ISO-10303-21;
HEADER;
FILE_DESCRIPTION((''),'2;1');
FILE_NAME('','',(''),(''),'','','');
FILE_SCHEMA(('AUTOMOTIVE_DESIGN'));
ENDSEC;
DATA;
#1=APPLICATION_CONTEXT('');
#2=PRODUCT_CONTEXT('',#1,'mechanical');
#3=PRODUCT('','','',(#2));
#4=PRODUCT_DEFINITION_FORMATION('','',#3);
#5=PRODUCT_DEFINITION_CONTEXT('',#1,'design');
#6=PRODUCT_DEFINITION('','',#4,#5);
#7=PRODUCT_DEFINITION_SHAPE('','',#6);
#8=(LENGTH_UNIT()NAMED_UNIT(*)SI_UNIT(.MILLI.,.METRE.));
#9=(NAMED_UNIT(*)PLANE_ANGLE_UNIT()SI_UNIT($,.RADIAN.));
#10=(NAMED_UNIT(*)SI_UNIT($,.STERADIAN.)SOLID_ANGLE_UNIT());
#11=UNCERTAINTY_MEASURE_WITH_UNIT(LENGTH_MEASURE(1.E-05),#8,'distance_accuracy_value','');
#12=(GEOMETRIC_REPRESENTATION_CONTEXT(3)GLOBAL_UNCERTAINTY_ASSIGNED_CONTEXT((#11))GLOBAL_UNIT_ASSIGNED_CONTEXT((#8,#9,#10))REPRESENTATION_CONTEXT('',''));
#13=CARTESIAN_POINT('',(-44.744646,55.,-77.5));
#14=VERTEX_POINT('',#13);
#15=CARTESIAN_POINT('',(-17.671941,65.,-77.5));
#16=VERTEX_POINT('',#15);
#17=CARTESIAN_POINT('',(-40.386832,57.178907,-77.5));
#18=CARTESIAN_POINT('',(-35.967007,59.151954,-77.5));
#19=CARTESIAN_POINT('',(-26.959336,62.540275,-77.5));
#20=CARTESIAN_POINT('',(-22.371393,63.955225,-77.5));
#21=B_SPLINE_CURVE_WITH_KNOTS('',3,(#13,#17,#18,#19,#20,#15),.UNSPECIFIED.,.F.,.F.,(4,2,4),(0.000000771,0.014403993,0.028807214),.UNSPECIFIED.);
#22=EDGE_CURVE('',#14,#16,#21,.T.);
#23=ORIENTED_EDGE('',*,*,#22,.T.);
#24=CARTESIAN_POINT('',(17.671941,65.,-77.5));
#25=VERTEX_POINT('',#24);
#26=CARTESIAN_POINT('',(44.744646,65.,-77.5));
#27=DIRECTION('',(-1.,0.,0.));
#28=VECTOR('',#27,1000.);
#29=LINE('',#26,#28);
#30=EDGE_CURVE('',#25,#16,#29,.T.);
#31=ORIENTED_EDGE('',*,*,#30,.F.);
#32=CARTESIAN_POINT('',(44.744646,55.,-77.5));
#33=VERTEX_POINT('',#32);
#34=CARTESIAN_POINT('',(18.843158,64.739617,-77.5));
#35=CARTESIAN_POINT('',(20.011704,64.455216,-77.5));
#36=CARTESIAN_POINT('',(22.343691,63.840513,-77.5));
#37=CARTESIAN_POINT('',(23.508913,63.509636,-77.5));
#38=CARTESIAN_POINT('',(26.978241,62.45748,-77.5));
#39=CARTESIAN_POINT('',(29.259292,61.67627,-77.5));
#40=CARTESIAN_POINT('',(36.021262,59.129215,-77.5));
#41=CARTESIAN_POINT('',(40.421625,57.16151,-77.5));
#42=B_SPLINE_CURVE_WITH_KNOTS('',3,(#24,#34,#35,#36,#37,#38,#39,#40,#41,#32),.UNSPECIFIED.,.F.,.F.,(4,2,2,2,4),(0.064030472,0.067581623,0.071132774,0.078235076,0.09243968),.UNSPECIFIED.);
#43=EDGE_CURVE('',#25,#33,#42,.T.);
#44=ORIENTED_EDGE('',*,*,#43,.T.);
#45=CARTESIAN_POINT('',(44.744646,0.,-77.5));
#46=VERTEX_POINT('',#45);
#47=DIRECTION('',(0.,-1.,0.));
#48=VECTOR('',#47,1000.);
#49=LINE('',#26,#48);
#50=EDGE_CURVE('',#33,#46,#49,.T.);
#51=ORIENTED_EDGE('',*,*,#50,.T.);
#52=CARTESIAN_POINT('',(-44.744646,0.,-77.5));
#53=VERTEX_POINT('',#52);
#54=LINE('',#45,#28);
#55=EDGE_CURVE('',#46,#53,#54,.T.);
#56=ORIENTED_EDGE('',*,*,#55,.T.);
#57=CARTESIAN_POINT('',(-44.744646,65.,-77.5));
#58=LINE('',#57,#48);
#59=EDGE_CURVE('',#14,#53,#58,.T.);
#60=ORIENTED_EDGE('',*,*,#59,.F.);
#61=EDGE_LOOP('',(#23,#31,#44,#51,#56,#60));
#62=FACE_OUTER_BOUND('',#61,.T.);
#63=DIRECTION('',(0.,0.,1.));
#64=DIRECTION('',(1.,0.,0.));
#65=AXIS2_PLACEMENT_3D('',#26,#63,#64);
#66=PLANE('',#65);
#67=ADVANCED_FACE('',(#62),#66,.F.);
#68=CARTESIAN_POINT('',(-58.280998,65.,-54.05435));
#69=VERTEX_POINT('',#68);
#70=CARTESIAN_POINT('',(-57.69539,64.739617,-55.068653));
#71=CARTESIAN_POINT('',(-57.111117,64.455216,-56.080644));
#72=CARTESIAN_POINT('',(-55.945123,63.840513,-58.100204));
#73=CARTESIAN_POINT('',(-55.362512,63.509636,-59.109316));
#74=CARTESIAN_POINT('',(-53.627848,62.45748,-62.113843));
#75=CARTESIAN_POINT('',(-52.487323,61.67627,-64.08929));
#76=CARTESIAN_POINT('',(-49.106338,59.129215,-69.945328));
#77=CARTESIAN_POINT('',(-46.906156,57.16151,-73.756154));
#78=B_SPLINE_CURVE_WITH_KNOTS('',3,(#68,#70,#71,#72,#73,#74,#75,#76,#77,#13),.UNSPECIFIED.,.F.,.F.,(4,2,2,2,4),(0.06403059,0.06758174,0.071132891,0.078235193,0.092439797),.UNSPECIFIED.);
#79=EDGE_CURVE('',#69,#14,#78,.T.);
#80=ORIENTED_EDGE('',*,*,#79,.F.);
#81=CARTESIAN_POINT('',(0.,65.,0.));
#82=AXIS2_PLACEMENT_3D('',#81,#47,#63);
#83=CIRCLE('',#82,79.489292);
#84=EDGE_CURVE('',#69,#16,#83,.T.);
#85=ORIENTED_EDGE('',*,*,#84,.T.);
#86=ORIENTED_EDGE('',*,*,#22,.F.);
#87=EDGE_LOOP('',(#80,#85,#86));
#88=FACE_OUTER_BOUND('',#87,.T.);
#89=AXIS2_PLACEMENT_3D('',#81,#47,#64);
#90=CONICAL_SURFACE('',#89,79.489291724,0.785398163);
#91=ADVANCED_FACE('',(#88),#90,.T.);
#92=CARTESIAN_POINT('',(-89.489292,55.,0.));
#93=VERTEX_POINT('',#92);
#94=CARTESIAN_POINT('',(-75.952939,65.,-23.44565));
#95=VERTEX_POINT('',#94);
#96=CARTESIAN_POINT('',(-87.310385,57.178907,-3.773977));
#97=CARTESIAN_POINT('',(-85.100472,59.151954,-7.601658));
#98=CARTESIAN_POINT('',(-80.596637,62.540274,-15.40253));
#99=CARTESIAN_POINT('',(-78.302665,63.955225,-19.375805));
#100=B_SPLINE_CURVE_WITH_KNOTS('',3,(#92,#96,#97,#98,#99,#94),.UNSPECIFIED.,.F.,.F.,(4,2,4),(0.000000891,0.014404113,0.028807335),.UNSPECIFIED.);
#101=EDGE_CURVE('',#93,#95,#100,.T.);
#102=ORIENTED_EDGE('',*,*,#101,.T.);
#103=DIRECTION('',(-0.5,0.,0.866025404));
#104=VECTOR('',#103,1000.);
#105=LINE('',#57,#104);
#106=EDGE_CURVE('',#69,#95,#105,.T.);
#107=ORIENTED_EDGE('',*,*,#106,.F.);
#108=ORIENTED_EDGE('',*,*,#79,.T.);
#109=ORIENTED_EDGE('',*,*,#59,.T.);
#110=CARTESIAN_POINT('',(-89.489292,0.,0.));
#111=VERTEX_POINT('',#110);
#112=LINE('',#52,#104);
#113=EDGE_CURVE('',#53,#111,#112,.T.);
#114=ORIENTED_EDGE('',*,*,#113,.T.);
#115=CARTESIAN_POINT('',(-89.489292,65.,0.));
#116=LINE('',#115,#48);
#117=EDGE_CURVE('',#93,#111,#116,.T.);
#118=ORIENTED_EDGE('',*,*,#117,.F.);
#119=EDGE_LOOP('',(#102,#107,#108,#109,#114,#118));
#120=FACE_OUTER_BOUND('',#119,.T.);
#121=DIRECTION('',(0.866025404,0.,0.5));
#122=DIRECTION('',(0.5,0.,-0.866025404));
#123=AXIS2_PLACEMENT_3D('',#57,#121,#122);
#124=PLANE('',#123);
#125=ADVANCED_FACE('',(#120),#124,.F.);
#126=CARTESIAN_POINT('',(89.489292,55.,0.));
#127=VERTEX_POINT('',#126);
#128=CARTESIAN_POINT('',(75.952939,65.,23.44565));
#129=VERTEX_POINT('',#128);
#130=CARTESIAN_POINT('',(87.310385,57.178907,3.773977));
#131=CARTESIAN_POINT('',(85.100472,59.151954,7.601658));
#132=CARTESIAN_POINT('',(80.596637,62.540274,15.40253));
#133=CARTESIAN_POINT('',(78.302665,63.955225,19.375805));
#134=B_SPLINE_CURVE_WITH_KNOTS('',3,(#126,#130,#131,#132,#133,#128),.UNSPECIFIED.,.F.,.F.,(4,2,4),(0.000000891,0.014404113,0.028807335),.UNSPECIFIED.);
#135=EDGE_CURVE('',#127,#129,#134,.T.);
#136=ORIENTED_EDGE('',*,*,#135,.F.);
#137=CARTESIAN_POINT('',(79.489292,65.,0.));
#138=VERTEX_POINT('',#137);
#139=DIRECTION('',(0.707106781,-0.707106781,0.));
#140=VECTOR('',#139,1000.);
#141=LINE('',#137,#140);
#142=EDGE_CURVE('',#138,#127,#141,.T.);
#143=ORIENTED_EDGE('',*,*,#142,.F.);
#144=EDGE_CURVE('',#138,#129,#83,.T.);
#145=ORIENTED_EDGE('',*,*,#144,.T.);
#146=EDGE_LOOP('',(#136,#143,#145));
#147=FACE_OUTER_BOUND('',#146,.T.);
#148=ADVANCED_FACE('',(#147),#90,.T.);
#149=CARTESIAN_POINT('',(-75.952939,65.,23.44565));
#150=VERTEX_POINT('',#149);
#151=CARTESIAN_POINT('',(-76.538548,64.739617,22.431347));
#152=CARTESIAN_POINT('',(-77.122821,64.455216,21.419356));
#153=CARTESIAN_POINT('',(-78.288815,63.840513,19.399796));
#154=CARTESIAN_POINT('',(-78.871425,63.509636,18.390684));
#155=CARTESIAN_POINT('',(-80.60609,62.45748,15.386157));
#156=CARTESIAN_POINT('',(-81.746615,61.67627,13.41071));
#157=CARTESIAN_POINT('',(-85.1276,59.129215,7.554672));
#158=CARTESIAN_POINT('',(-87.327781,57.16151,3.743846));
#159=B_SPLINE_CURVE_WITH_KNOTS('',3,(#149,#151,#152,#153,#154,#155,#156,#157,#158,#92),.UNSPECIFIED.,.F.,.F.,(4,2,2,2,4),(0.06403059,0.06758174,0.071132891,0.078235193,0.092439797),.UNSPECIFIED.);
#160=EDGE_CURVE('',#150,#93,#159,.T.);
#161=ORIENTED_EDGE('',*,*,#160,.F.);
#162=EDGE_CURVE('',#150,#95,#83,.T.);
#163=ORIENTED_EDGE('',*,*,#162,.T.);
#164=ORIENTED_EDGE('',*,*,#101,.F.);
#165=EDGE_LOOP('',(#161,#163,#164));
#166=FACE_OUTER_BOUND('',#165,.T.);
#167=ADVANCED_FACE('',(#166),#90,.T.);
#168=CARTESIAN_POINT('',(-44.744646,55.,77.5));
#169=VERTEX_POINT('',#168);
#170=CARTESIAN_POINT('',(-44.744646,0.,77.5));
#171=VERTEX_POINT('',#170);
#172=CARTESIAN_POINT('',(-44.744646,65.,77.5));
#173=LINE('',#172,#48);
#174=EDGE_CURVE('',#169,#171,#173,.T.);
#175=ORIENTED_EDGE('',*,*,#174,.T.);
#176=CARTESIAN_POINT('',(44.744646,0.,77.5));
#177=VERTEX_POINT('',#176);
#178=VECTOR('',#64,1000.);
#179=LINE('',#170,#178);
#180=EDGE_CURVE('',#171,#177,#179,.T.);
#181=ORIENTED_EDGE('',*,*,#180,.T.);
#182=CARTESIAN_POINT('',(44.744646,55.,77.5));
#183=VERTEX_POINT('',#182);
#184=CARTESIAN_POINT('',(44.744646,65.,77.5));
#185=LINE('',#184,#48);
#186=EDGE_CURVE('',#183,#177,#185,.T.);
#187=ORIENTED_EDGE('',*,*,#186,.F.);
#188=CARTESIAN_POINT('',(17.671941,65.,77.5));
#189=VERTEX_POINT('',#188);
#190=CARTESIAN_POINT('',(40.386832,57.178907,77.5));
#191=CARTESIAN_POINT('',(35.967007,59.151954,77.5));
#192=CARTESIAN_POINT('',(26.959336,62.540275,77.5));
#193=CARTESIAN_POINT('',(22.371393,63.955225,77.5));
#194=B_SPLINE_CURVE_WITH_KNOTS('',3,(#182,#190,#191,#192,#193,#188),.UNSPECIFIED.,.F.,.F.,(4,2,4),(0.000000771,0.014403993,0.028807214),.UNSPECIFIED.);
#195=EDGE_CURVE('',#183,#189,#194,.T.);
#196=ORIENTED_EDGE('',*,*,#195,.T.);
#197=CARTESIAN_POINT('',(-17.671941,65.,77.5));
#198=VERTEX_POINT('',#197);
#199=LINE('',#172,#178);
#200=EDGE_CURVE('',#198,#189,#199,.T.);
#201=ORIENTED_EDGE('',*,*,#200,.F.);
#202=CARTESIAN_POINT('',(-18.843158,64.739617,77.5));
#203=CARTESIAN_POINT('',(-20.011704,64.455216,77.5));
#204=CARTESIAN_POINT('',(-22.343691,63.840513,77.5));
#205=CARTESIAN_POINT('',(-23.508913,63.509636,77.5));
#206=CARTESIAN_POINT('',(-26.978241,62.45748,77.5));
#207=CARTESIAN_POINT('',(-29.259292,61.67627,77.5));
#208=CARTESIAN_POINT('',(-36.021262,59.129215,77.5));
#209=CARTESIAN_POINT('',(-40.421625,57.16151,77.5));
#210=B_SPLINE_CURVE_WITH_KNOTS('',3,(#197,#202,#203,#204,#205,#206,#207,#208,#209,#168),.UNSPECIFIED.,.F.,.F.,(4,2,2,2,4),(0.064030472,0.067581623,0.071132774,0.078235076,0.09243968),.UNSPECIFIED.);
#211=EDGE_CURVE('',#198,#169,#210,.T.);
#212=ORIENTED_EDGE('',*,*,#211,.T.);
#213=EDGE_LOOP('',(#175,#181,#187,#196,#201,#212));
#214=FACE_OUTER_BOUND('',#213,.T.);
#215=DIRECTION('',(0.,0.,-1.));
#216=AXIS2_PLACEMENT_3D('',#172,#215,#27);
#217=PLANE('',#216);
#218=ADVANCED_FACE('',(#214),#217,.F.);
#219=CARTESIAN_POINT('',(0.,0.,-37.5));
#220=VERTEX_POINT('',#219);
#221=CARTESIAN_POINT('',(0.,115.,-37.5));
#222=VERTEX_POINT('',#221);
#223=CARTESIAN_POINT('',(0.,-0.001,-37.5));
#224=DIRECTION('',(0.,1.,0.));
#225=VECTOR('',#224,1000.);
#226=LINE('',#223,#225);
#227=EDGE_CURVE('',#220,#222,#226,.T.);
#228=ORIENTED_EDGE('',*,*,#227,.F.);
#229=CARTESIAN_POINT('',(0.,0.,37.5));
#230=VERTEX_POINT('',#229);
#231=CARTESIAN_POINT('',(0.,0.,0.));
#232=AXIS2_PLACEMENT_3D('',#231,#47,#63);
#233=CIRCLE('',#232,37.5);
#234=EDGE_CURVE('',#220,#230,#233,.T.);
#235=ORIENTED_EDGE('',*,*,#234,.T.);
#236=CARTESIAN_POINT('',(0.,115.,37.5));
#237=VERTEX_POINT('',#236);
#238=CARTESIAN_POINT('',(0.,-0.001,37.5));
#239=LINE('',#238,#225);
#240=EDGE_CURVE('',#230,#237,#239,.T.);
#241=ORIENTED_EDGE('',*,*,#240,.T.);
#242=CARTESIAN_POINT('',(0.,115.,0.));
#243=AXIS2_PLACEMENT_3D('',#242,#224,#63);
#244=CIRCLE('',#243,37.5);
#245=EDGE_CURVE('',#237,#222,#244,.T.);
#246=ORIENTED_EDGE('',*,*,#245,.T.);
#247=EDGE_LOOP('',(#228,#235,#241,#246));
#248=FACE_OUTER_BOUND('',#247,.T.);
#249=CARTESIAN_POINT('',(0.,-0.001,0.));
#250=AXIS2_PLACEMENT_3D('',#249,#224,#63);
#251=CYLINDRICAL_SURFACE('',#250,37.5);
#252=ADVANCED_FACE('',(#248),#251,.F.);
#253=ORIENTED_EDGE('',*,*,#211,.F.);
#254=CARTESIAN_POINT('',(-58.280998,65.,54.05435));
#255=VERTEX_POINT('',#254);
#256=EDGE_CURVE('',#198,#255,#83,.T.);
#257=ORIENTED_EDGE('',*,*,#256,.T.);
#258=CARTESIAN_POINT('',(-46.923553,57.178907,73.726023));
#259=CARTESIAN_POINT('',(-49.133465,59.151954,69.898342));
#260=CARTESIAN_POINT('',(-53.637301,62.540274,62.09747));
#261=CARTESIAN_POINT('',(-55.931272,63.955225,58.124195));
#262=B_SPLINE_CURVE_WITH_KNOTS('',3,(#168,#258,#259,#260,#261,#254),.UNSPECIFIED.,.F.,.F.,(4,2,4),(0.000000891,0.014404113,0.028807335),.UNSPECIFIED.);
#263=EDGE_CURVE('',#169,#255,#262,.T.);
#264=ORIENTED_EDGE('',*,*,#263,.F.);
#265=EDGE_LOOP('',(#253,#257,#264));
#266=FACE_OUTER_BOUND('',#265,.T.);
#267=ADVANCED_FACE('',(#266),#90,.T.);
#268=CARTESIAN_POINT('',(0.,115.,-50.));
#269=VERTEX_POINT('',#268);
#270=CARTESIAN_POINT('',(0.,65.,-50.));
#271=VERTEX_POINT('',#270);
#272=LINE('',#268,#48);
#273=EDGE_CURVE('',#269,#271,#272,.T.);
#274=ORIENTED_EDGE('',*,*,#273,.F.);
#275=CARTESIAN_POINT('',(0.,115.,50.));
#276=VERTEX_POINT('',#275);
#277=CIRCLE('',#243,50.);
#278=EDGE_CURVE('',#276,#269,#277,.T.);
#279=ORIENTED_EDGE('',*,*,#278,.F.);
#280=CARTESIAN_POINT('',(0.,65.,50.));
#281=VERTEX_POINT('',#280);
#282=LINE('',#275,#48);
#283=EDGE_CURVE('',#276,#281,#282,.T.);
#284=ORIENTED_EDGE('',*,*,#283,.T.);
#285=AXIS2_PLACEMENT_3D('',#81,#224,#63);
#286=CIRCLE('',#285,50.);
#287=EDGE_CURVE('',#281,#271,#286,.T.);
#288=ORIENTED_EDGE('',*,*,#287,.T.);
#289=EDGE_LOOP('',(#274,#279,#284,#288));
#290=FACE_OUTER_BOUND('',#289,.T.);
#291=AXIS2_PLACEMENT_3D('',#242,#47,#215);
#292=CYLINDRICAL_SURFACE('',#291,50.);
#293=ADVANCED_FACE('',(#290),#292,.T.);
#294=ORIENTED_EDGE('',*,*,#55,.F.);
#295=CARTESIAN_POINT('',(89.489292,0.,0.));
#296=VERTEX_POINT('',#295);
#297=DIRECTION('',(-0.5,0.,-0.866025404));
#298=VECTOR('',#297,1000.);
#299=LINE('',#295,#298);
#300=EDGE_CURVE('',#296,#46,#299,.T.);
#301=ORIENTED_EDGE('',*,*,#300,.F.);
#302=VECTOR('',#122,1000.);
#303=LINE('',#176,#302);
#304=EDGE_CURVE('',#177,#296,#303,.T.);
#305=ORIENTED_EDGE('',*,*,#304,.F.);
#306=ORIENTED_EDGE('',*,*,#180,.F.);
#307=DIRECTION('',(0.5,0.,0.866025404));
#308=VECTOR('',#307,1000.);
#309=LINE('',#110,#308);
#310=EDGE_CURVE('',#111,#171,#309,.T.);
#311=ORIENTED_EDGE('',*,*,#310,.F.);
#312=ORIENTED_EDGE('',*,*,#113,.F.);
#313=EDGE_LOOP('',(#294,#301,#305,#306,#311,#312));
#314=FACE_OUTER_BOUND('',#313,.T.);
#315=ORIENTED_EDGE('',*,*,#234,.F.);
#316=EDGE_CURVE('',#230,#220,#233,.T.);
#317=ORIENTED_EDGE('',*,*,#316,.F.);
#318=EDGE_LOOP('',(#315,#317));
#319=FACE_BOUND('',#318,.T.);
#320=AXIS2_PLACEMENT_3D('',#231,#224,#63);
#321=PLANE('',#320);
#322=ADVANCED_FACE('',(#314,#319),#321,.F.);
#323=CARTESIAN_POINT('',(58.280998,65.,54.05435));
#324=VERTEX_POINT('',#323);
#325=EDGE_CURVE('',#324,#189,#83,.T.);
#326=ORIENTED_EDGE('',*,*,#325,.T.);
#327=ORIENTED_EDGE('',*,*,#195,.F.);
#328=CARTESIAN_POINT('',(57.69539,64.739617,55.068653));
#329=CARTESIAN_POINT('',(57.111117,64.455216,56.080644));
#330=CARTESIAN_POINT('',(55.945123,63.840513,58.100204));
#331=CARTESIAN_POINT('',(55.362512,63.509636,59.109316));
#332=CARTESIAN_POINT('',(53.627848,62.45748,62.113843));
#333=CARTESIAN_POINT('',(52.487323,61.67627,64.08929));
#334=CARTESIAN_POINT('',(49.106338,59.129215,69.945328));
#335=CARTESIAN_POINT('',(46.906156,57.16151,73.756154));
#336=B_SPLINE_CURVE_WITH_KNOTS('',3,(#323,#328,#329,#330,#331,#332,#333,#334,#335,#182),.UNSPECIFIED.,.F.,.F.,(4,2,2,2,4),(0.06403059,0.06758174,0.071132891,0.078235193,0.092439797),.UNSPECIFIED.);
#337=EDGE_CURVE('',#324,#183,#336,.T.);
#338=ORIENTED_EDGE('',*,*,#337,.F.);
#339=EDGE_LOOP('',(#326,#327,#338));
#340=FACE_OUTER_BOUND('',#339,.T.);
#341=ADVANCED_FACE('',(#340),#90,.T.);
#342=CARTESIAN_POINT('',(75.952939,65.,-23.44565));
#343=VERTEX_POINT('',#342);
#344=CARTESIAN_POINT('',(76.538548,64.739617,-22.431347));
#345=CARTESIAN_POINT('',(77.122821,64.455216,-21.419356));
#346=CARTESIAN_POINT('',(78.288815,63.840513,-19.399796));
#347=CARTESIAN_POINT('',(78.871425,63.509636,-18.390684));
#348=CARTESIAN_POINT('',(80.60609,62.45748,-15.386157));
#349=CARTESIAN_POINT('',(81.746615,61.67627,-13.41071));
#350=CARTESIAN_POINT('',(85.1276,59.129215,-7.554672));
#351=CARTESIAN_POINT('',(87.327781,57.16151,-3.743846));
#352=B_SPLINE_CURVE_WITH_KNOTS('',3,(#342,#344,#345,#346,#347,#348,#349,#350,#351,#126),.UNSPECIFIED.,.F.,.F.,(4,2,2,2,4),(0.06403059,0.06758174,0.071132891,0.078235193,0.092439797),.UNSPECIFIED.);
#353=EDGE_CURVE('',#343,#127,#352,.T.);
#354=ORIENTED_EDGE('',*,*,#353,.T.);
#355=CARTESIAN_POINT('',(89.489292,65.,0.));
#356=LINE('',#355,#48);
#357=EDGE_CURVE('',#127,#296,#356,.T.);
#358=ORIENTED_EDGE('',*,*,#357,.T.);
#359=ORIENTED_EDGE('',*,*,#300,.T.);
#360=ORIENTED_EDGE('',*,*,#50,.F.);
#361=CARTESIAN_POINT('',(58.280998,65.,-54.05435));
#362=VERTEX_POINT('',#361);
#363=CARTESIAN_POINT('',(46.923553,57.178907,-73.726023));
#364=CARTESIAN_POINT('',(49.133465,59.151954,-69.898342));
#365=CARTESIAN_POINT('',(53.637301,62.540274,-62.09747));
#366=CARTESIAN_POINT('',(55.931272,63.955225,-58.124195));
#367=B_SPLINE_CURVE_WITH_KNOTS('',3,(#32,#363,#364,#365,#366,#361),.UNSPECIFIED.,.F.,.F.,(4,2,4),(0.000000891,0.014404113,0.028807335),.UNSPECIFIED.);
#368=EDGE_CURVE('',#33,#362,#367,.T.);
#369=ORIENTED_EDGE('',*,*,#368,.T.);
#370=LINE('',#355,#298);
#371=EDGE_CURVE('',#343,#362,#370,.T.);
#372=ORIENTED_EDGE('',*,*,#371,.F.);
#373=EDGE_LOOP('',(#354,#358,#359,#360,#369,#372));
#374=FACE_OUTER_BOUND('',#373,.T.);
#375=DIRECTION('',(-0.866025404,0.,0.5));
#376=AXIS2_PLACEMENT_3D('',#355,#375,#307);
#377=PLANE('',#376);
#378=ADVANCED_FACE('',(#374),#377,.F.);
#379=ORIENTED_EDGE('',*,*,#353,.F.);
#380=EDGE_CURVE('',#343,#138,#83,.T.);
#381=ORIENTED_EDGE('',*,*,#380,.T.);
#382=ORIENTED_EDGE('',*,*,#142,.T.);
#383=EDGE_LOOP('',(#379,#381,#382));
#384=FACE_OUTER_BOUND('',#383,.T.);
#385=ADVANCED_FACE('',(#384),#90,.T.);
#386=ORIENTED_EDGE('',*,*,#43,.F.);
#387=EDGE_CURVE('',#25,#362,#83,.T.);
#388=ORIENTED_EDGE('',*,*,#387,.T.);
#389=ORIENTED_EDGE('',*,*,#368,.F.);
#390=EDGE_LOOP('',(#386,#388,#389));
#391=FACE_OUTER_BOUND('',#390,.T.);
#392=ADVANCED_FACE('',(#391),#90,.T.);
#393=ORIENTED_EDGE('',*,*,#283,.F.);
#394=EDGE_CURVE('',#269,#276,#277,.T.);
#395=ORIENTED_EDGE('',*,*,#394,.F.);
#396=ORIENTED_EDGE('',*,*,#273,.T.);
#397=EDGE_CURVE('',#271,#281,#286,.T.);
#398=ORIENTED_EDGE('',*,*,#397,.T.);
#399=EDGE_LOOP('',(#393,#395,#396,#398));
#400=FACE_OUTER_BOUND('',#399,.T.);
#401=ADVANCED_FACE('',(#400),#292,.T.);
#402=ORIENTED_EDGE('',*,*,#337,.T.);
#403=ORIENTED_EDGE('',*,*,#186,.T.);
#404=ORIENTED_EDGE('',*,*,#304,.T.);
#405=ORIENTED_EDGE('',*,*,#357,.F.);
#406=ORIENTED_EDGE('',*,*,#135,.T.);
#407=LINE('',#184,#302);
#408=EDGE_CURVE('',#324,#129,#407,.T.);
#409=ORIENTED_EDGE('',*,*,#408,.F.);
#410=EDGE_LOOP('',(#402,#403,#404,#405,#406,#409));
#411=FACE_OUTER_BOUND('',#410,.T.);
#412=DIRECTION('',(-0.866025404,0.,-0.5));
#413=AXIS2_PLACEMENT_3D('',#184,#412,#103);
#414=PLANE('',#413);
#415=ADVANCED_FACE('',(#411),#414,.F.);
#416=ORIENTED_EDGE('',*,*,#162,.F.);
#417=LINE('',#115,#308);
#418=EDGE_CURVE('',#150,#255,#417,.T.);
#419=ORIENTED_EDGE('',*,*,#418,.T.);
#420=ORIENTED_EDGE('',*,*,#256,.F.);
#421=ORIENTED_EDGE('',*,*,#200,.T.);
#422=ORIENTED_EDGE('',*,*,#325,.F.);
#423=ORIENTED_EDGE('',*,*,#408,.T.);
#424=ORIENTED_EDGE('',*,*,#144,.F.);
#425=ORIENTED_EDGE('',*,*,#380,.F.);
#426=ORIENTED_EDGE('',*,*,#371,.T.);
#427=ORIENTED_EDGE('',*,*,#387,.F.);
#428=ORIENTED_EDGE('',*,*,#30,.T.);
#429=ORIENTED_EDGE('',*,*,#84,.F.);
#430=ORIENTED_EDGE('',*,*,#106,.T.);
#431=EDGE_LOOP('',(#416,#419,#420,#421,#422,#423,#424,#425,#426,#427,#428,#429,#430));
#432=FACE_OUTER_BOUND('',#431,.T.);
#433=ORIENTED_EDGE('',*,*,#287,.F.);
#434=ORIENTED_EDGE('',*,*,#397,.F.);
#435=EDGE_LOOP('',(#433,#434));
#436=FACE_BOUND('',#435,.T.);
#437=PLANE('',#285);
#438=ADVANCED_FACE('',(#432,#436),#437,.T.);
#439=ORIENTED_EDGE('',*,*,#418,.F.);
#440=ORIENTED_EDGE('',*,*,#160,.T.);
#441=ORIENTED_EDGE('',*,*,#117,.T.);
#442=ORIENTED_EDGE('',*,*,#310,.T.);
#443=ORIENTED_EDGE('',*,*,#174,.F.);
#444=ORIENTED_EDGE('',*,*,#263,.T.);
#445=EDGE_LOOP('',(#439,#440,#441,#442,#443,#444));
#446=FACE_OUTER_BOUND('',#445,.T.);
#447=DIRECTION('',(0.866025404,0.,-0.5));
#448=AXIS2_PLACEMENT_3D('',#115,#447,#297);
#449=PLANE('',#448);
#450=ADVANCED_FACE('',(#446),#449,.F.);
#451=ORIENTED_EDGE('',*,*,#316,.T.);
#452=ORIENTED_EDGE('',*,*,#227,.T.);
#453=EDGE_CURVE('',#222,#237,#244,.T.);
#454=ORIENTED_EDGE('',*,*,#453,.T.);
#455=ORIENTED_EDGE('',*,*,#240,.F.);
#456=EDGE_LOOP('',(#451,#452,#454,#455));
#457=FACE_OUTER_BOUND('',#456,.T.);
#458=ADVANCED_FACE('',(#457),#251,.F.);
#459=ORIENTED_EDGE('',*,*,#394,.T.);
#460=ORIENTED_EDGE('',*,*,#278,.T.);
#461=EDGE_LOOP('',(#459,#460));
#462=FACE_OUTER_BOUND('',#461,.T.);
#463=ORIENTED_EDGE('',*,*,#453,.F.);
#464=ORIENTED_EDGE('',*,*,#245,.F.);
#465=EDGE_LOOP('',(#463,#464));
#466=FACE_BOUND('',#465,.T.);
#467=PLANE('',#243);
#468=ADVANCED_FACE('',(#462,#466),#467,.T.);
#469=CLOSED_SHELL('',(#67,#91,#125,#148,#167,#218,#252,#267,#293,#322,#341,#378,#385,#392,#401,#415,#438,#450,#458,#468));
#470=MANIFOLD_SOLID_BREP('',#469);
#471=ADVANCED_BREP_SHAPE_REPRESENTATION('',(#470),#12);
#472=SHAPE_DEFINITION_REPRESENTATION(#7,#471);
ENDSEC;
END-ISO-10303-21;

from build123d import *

# Parameters (mm, degrees)
HEX_BODY_155AF_X65_DEPTH = 65
COLLAR_PROFILE_100_R     = 50
COLLAR_100_X50_DEPTH     = 50
THROUGH_BORE_75_REACH    = 167.044
BORE_PROFILE_75_R        = 37.5


with BuildPart() as part:
    # Hex Profile 155AF → Hex Body 155AF x65 (new body)
    with BuildSketch(Plane(origin=(0, 0, 0), x_dir=(1, 0, 0), z_dir=(0, 1, 0))):
        Polygon((89.489291724, 0), (44.744645862, 77.5), (-44.744645862, 77.5), (-89.489291724, 0), (-44.744645862, -77.5), (44.744645862, -77.5), align=None)
    extrude(amount=HEX_BODY_155AF_X65_DEPTH)

    # Hex Chamfer Profile 10x10 → Hex Corner Chamfer 10x10 (revolve, cut)
    with BuildSketch(Plane.XY):
        Polygon((79.489291724, 65), (89.489291724, 65), (89.489291724, 55), align=None)
    revolve(axis=Axis((0, 0, 0), (0, 1, 0)), mode=Mode.SUBTRACT)

    # Collar Profile Ø100 → Collar Ø100 x50 (add)
    with BuildSketch(Plane(origin=(0, 65, 0), x_dir=(1, 0, 0), z_dir=(0, 1, 0))):
        with Locations(Location((0, 0, 0), (0, 0, 270))):
            Circle(COLLAR_PROFILE_100_R)
    extrude(amount=COLLAR_100_X50_DEPTH)

    # Bore Profile Ø75 → Through Bore Ø75 (cut, up to next)
    with BuildSketch(Plane(origin=(0, 115, 0), x_dir=(1, 0, 0), z_dir=(0, 1, 0)), mode=Mode.PRIVATE) as through_bore_75_sk1:
        with Locations(Location((0, 0, 0), (0, 0, 270))):
            Circle(BORE_PROFILE_75_R)
    through_bore_75_tool1 = extrude(through_bore_75_sk1.sketch, amount=-THROUGH_BORE_75_REACH, mode=Mode.PRIVATE) & part.part
    add(through_bore_75_tool1.solids().sort_by_distance((0, 115, 0))[0], mode=Mode.SUBTRACT)


solid = part.part
